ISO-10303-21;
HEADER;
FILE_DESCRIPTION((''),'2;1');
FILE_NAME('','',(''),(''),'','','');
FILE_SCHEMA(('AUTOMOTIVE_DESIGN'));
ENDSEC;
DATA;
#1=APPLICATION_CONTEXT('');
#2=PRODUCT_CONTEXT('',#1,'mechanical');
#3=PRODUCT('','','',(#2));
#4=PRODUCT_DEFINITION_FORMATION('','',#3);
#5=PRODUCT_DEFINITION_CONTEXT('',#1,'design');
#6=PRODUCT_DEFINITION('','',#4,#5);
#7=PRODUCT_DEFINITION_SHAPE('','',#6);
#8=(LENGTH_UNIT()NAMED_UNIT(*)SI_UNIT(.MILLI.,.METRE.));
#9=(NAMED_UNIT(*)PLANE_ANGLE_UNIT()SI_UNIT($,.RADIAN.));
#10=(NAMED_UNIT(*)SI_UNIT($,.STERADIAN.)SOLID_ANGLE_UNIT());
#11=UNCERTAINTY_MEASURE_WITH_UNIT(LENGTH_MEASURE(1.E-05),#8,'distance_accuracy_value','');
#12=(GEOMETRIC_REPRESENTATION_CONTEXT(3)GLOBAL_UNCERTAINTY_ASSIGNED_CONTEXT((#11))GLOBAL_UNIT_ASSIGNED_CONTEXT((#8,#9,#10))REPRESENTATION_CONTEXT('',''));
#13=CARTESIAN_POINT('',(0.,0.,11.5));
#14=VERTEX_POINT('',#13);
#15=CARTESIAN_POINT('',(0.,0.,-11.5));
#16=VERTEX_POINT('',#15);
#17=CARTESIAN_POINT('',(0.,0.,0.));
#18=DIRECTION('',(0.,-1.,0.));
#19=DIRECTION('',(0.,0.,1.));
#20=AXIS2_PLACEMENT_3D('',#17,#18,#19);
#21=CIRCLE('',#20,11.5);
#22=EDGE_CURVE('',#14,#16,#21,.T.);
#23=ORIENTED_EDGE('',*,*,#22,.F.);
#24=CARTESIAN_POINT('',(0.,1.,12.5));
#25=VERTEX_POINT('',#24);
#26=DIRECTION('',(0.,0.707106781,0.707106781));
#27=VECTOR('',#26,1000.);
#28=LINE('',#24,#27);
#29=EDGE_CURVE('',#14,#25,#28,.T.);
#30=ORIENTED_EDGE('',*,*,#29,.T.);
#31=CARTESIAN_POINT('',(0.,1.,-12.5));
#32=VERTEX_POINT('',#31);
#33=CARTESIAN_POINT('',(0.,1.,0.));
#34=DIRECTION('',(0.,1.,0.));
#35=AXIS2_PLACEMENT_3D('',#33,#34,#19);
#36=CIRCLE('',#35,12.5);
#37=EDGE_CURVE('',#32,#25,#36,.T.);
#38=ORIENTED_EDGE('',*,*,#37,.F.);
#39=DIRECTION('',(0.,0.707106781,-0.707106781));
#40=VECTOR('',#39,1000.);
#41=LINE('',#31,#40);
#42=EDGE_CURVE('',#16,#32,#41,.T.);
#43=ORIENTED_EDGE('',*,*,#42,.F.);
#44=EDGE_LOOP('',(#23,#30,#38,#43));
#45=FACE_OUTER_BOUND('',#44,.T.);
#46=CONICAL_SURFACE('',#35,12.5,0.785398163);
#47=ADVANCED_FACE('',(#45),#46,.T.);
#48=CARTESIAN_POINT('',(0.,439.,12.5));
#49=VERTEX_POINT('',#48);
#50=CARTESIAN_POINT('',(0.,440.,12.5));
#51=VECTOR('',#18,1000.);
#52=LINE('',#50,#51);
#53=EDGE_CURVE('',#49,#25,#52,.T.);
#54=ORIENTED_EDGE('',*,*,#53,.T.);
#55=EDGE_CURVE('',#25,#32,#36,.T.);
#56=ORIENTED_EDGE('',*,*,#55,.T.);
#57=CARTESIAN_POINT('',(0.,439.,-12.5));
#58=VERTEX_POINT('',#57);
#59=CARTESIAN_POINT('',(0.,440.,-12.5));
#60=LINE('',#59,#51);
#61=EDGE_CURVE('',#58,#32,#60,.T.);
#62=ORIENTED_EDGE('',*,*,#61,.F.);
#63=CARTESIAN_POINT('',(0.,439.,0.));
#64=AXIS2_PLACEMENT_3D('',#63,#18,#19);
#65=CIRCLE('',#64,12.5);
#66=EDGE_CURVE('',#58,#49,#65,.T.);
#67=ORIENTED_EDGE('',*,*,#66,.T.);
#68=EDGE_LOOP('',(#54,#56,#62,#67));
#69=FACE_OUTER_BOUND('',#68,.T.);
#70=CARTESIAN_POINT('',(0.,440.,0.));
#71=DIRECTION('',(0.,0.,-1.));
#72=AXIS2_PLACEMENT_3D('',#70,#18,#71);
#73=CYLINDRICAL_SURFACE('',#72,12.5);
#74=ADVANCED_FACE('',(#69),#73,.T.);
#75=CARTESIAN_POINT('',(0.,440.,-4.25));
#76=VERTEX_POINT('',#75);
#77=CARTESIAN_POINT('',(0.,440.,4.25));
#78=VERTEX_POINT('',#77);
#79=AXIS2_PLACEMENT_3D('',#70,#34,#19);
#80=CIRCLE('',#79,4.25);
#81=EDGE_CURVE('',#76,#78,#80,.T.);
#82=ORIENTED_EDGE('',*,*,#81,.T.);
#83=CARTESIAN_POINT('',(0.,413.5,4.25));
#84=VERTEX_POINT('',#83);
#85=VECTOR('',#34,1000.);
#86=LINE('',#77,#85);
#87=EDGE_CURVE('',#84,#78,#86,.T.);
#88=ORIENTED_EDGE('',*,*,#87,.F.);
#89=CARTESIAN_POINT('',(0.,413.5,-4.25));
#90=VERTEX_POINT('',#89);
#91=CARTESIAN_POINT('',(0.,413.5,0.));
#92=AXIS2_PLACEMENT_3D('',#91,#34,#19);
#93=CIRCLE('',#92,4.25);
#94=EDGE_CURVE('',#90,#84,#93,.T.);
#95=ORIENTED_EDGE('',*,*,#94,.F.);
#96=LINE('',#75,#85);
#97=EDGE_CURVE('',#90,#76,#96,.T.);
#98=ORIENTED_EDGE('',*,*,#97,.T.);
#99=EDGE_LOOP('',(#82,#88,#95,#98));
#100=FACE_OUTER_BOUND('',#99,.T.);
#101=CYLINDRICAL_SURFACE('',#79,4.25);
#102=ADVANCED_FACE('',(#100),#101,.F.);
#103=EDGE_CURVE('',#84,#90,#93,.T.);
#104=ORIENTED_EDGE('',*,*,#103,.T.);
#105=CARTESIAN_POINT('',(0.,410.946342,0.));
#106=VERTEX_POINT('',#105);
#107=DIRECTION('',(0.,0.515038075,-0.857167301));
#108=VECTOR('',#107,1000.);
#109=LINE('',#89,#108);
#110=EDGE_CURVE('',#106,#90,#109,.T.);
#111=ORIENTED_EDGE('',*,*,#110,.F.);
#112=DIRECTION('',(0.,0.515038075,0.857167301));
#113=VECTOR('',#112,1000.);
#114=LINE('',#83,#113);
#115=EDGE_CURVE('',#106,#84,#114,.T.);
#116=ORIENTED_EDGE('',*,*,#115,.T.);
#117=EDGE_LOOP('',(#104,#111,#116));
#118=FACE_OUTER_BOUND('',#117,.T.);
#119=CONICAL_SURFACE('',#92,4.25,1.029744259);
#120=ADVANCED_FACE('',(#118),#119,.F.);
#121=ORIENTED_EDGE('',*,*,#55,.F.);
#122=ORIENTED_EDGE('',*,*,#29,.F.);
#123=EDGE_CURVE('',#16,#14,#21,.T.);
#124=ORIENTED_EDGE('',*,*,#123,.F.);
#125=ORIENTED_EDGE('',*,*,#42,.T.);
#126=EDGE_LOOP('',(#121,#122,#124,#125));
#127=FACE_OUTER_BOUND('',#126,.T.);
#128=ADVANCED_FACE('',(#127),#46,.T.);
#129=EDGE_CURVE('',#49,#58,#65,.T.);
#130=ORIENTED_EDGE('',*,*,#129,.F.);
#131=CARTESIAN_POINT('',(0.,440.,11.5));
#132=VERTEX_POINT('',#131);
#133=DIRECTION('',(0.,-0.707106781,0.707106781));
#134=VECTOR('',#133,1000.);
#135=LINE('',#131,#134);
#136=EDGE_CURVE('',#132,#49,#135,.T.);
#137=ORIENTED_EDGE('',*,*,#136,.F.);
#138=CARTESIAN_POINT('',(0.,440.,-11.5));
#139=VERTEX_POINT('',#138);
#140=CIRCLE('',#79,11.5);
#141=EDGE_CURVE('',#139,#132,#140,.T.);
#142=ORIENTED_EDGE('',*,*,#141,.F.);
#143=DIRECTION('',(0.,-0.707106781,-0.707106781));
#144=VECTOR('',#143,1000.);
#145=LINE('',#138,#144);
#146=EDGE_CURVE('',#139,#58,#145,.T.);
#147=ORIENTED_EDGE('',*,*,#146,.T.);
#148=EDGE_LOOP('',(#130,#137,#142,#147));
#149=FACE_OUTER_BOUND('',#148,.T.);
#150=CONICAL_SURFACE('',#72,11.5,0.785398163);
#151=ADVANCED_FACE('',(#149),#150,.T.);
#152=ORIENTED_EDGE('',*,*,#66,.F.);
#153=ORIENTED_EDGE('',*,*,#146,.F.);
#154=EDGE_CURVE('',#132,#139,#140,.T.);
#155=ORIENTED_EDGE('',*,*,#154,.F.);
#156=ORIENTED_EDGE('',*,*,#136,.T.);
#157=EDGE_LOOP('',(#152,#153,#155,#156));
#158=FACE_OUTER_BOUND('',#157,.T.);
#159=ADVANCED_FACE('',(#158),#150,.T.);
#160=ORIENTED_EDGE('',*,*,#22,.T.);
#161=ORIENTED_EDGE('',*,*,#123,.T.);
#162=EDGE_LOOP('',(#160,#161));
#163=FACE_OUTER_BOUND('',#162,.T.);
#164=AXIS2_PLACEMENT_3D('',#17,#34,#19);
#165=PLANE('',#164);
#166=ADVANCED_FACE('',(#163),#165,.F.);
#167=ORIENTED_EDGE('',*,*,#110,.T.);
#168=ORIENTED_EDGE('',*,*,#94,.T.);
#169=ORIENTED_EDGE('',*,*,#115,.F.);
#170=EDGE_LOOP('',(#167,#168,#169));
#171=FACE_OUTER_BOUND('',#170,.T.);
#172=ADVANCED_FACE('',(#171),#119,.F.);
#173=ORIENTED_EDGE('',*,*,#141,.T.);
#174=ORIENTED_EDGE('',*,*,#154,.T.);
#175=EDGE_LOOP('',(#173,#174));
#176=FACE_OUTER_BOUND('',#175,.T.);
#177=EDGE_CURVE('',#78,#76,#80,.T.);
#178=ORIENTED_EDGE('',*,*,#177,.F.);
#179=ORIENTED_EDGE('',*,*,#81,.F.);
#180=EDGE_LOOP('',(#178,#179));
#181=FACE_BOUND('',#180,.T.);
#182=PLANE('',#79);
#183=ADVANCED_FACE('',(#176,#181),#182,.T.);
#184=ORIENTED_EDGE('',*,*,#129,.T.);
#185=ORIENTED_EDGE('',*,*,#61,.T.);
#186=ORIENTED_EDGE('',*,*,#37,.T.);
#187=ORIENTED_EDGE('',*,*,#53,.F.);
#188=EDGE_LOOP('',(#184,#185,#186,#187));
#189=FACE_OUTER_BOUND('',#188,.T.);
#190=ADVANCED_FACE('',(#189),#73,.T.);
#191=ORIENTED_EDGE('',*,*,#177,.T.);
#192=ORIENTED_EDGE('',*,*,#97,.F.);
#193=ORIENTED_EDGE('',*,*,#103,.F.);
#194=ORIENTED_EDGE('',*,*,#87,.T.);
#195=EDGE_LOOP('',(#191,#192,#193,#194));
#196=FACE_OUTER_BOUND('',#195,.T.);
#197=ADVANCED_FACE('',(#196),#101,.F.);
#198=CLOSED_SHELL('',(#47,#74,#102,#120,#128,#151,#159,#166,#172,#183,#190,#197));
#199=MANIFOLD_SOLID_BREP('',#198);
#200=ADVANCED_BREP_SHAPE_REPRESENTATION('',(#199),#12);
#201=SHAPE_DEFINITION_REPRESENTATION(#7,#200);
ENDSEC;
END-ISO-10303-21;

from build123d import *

# Parameters (mm, degrees)
SKETCH_1_R              = 12.5
EXTRUDE_1_DEPTH         = 440
CHAMFER_1_SIZE          = 1
HOLE_WIZARD_M10_1_D     = 8.5
HOLE_WIZARD_M10_1_DEPTH = 26.5
HOLE_WIZARD_M10_1_TIP   = 2.553657631


with BuildPart() as part:
    # 草图1 → 凸台-拉伸1 (new body)
    with BuildSketch(Plane(origin=(0, 0, 0), x_dir=(1, 0, 0), z_dir=(0, 1, 0))):
        with Locations(Location((0, 0, 0), (0, 0, 270))):
            Circle(SKETCH_1_R)
    extrude(amount=EXTRUDE_1_DEPTH)

    # 倒角1
    chamfer_1_edges = [part.edges().sort_by_distance(p)[0] for p in [
        (0, 0, -12.5),
        (0, 440, -12.5),
    ]]
    chamfer(chamfer_1_edges, length=CHAMFER_1_SIZE)

    # M10 螺纹孔1
    with Locations(Plane(origin=(0, 440, 0), x_dir=(1, 0, 0), z_dir=(0, 1, 0))):
        with Locations((0, 0)):
            Hole(HOLE_WIZARD_M10_1_D / 2, depth=HOLE_WIZARD_M10_1_DEPTH)
            with Locations((0, 0, -(HOLE_WIZARD_M10_1_DEPTH + HOLE_WIZARD_M10_1_TIP / 2))):  # 118° drill point
                Cone(0, HOLE_WIZARD_M10_1_D / 2, HOLE_WIZARD_M10_1_TIP, mode=Mode.SUBTRACT)


solid = part.part
